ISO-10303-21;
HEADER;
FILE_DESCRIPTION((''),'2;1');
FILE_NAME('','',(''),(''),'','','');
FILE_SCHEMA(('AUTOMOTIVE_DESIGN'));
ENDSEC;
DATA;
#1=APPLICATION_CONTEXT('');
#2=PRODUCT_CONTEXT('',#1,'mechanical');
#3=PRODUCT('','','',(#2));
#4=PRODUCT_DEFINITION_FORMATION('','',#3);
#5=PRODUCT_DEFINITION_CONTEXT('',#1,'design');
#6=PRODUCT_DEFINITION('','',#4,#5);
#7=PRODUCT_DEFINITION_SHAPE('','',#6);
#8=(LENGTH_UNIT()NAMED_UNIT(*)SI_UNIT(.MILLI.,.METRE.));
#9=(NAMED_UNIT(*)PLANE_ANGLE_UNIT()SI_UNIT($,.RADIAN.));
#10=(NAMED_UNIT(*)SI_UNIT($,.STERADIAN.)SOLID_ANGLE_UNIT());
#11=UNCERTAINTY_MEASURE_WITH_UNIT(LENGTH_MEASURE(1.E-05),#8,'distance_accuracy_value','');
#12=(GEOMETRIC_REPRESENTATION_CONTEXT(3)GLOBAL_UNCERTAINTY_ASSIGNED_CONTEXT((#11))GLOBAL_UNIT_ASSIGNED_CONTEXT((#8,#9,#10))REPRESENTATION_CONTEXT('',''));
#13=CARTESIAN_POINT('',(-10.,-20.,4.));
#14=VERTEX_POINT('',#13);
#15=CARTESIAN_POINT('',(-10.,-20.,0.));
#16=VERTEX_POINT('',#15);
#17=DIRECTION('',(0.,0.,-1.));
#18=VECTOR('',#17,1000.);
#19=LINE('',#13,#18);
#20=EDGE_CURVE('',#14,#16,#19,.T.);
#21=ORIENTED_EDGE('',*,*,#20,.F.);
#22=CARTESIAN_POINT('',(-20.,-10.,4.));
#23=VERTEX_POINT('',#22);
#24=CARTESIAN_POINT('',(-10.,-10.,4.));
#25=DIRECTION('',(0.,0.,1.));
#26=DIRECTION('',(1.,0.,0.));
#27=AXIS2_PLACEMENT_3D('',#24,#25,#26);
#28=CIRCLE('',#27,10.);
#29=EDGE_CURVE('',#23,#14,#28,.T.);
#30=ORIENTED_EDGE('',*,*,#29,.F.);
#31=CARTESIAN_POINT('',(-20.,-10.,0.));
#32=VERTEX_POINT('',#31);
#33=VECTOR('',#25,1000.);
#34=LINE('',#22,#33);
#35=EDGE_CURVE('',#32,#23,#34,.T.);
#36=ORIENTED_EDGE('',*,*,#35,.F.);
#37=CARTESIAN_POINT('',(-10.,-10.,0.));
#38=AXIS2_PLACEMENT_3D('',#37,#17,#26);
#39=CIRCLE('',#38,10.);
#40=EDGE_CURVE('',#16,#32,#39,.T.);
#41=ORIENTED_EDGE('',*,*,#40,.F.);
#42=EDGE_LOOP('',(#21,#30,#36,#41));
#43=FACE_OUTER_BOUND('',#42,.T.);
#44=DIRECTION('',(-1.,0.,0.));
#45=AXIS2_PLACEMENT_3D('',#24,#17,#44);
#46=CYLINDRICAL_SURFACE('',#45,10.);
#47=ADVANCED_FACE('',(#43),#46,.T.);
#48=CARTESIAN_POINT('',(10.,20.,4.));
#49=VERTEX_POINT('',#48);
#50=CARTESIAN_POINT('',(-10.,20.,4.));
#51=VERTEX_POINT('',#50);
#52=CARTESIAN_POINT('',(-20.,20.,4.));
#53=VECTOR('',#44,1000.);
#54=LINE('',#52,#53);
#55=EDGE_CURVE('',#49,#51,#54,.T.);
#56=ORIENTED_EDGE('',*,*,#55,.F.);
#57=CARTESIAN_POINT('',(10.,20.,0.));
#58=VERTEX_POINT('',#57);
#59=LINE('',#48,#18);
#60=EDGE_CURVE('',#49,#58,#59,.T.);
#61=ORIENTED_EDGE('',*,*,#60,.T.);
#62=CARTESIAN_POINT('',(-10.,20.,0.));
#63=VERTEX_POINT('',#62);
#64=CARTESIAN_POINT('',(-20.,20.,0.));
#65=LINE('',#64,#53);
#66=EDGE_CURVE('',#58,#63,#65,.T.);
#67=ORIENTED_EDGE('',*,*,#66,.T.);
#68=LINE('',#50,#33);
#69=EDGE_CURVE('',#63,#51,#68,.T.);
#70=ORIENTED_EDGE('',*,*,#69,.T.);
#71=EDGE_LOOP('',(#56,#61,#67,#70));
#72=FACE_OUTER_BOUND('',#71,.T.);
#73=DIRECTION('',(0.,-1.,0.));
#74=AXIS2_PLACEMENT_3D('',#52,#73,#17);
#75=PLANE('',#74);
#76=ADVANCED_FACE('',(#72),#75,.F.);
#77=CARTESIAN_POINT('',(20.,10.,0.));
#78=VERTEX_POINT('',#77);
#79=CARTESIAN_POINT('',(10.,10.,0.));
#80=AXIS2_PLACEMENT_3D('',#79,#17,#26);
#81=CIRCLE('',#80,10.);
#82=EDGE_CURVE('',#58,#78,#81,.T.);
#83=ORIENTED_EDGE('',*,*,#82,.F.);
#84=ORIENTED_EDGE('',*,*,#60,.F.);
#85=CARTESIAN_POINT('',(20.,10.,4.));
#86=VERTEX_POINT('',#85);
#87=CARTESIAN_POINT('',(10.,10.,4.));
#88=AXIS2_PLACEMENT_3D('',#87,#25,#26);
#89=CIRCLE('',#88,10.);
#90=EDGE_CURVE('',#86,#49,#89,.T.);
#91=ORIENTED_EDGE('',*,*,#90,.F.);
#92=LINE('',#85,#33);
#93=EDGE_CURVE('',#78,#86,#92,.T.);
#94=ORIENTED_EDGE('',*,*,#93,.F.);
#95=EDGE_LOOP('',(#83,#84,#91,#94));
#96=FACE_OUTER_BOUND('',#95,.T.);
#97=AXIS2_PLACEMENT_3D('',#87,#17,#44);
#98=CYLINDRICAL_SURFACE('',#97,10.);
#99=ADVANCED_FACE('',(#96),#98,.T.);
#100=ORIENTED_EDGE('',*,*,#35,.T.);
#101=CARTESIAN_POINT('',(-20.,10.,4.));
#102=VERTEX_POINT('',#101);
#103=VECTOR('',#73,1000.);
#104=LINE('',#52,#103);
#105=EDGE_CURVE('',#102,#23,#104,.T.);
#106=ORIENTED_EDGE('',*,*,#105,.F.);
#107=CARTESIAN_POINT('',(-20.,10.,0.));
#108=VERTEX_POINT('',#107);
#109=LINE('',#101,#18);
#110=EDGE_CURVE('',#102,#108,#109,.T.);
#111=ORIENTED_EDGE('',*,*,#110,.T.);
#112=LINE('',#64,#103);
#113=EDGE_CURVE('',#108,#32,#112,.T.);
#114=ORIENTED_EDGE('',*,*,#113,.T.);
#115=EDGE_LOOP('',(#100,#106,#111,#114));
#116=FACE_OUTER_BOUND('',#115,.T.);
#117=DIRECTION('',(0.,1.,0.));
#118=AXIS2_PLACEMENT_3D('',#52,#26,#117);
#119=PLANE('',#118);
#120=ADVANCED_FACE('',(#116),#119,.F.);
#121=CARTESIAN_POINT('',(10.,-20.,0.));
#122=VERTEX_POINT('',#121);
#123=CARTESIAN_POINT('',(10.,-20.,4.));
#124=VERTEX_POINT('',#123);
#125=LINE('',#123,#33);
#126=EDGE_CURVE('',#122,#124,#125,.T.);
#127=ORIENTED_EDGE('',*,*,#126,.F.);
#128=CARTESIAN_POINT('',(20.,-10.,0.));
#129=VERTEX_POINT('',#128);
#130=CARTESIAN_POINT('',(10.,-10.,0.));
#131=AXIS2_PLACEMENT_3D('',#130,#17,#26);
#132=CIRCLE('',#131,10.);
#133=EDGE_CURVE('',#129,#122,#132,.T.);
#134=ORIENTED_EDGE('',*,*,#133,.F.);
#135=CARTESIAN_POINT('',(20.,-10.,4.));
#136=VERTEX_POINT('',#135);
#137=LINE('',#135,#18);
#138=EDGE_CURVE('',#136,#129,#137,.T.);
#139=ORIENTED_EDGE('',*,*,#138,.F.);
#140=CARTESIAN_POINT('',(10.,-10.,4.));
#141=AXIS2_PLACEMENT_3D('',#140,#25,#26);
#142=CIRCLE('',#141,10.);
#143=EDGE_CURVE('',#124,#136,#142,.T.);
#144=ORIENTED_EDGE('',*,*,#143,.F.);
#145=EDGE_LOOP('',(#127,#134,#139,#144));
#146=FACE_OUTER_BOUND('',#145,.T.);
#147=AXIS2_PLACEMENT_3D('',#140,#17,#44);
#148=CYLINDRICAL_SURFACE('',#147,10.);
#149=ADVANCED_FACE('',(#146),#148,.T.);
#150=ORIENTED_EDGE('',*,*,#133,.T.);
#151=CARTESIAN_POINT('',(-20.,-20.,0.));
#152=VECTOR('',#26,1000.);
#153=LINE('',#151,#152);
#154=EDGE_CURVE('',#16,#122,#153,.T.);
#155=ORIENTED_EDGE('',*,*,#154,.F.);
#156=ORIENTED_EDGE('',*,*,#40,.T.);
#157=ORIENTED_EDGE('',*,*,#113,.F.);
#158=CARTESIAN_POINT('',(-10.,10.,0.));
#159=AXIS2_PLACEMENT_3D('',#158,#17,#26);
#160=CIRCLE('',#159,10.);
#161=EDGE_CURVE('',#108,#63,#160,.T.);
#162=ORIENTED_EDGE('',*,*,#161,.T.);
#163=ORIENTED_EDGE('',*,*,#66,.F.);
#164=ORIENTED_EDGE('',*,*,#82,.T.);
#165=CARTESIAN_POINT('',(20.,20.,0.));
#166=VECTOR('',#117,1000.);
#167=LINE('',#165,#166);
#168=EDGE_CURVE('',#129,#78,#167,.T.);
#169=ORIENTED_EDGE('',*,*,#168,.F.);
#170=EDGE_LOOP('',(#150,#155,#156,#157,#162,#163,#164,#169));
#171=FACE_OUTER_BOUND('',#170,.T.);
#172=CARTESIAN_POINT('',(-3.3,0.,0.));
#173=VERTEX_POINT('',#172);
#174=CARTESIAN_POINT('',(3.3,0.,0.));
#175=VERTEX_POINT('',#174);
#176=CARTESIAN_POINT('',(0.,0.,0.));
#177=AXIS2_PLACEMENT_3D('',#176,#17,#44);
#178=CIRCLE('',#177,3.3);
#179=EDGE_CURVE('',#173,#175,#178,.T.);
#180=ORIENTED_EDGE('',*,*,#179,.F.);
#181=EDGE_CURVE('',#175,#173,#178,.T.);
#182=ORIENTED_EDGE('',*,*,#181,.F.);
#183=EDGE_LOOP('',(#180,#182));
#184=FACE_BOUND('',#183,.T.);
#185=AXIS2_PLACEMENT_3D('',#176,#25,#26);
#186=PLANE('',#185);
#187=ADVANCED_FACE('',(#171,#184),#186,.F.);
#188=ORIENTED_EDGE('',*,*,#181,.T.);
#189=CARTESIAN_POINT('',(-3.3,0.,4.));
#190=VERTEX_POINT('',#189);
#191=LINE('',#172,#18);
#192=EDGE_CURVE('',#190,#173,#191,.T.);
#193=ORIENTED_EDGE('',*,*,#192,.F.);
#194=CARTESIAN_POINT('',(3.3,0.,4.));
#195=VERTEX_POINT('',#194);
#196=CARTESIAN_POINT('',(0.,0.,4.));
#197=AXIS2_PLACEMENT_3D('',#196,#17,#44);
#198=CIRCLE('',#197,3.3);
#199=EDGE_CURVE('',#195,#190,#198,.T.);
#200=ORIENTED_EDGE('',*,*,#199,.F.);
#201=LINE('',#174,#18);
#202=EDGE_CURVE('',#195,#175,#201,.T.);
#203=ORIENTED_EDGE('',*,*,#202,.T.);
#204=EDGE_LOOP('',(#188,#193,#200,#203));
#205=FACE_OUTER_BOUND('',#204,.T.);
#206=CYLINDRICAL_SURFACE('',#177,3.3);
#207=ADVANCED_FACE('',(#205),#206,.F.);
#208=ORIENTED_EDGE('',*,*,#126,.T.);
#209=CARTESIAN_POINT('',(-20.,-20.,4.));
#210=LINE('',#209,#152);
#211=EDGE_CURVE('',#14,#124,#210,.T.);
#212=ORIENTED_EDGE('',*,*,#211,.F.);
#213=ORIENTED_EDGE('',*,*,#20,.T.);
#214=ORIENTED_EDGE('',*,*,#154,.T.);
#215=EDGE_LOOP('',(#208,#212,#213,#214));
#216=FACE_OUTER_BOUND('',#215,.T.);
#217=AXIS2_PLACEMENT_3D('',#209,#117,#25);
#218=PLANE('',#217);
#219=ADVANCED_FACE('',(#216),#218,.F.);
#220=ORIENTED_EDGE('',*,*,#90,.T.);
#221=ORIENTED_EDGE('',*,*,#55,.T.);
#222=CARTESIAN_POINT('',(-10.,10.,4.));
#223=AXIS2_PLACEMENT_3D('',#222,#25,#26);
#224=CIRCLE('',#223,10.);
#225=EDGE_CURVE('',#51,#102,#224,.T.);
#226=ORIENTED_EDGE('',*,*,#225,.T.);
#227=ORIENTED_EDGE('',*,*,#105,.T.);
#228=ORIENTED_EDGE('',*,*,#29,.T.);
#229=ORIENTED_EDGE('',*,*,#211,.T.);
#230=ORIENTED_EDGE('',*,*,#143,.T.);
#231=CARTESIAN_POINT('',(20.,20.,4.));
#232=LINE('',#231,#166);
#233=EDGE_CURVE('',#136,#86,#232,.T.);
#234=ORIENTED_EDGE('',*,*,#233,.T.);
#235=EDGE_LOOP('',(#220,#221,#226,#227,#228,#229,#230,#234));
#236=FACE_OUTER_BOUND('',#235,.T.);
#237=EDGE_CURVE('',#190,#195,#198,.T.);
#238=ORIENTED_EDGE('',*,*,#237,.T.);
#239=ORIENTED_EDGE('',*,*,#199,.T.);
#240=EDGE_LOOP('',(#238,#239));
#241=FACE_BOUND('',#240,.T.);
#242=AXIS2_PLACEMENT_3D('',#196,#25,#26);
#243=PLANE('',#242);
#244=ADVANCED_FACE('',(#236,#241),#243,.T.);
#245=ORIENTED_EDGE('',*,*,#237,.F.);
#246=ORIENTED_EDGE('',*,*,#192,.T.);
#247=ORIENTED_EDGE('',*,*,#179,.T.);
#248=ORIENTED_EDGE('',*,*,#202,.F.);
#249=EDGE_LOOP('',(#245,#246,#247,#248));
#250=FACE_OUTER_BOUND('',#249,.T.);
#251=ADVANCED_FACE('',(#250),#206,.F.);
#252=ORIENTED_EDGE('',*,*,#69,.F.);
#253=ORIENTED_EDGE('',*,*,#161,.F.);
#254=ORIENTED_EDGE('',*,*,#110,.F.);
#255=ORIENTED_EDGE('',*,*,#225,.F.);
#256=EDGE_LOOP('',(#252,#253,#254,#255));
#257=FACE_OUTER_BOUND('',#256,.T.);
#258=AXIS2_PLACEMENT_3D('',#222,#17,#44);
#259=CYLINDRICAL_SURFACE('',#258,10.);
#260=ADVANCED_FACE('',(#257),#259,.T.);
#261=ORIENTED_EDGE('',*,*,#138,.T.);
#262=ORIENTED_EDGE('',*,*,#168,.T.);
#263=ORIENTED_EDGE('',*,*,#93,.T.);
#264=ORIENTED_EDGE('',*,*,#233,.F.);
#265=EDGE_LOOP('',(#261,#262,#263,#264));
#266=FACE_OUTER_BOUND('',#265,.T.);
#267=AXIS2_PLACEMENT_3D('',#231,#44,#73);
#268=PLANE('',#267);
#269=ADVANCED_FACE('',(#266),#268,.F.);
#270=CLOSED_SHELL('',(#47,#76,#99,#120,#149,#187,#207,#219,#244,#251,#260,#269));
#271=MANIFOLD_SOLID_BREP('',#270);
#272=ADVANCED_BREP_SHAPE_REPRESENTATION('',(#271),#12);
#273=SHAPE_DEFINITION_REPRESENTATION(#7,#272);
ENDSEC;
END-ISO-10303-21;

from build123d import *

# Parameters (mm, degrees)
SKETCH_1_W         = 40
SKETCH_1_H         = 40
EXTRUDE_1_DEPTH    = 4
FILLET_1_R         = 10
HOLE_WIZARD_M6_1_D = 6.6


with BuildPart() as part:
    # 草图1 → 凸台-拉伸1 (new body)
    with BuildSketch(Plane.XY):
        Rectangle(SKETCH_1_W, SKETCH_1_H)
    extrude(amount=EXTRUDE_1_DEPTH)

    # 圆角1
    fillet_1_edges = [part.edges().sort_by_distance(p)[0] for p in [
        (20, -20, 2),
        (-20, -20, 2),
        (-20, 20, 2),
        (20, 20, 2),
    ]]
    fillet(fillet_1_edges, radius=FILLET_1_R)

    # Hole Wizard M6 _1 (through all)
    with Locations(Plane(origin=(0, 0, 0), x_dir=(-1, 0, 0), z_dir=(0, 0, -1))):
        with Locations((0, 0)):
            Hole(HOLE_WIZARD_M6_1_D / 2)


solid = part.part
